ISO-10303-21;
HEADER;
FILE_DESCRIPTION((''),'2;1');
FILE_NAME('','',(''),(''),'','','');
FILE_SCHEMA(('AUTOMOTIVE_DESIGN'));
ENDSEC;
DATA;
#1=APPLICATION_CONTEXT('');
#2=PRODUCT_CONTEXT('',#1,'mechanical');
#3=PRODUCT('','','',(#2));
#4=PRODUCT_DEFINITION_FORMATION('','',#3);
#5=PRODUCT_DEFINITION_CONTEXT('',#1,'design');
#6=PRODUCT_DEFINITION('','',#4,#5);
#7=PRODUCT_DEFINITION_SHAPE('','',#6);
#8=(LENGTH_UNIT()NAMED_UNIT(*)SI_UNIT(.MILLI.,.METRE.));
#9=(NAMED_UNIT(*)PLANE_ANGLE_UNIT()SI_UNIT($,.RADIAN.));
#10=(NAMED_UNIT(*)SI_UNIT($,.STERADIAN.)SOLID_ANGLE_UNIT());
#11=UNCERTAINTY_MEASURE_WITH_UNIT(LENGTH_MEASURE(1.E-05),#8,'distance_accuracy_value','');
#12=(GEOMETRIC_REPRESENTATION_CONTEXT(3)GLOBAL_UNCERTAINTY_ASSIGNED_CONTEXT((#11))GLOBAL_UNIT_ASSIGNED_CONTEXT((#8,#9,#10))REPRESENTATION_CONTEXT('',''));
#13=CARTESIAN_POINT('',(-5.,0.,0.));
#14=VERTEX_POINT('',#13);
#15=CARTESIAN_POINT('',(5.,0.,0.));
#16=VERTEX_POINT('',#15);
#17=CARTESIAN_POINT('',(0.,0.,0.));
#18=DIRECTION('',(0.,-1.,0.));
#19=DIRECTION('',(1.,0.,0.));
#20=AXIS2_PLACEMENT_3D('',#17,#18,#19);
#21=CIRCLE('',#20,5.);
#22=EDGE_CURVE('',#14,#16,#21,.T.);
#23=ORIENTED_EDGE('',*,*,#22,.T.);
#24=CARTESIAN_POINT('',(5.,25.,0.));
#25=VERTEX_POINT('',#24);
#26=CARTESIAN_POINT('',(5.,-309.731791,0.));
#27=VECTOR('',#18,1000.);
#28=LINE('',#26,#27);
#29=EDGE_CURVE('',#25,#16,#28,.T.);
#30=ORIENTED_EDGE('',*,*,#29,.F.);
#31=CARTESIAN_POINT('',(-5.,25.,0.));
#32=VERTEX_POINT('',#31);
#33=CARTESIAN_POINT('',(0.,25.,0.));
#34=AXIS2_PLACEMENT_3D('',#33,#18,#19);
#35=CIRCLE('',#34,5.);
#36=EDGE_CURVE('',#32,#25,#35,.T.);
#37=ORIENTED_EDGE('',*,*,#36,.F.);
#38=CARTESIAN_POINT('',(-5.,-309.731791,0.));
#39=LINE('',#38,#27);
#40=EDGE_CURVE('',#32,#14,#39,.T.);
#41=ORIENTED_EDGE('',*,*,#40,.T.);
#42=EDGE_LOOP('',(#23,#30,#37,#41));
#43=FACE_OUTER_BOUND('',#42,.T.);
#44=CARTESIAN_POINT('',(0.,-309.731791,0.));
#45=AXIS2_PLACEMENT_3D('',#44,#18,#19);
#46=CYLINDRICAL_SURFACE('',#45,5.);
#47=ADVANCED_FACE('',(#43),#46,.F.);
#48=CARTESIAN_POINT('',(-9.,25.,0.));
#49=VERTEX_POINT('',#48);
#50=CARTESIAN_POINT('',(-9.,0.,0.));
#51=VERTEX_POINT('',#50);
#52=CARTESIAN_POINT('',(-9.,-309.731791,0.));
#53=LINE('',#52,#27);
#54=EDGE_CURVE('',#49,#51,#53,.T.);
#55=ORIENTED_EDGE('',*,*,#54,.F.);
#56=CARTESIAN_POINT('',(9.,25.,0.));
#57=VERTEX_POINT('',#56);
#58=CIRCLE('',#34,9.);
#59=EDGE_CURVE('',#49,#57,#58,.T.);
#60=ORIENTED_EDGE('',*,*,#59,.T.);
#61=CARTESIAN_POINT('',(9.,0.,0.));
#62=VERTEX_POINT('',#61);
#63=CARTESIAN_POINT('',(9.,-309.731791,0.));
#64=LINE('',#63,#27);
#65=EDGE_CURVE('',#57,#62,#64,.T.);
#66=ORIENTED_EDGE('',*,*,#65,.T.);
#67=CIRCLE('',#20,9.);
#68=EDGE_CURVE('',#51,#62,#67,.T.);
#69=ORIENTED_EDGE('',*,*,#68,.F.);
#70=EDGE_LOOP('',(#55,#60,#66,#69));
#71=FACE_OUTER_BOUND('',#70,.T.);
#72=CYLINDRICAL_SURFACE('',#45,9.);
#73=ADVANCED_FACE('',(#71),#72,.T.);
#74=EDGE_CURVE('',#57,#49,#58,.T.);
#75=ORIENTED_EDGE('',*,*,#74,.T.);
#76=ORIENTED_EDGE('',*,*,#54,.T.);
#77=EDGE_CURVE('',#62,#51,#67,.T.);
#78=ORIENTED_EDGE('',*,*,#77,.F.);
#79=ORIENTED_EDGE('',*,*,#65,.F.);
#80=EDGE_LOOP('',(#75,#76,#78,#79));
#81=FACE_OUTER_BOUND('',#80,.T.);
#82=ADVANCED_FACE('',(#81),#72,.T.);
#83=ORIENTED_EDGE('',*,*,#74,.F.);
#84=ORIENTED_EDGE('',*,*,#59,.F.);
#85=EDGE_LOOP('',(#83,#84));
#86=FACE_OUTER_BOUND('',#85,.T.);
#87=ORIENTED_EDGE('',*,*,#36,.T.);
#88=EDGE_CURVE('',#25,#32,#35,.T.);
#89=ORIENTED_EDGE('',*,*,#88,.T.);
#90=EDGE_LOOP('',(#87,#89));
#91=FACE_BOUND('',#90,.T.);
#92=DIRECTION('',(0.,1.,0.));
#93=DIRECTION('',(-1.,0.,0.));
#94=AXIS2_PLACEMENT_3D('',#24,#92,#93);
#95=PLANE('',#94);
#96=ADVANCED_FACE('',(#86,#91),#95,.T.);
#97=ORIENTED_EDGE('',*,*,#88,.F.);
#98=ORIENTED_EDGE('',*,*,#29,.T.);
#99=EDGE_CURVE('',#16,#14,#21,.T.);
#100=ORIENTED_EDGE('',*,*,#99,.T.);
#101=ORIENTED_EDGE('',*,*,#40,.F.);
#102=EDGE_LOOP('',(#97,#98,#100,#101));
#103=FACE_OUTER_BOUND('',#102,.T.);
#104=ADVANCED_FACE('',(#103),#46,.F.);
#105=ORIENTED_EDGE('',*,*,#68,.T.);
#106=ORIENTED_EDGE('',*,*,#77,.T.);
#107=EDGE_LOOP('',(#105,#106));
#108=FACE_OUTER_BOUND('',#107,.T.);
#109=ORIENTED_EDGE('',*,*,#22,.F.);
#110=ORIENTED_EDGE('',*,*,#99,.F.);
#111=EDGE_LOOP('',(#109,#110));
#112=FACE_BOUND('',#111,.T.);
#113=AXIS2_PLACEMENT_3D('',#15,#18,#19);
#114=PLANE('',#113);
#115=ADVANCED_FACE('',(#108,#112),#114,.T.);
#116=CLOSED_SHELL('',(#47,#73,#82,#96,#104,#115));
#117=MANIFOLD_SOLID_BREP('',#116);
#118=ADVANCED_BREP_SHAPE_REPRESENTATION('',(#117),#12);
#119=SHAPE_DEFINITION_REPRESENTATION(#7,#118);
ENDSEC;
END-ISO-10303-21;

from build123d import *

# Parameters (mm, degrees)
SKETCH1_W = 4
SKETCH1_H = 25


with BuildPart() as part:
    # Sketch1 → Revolve1 (revolve)
    with BuildSketch(Plane.XY):
        with Locations((7, 12.5)):
            Rectangle(SKETCH1_W, SKETCH1_H)
    revolve(axis=Axis((0, -309.731791339, 0), (0, 1, 0)))


solid = part.part
